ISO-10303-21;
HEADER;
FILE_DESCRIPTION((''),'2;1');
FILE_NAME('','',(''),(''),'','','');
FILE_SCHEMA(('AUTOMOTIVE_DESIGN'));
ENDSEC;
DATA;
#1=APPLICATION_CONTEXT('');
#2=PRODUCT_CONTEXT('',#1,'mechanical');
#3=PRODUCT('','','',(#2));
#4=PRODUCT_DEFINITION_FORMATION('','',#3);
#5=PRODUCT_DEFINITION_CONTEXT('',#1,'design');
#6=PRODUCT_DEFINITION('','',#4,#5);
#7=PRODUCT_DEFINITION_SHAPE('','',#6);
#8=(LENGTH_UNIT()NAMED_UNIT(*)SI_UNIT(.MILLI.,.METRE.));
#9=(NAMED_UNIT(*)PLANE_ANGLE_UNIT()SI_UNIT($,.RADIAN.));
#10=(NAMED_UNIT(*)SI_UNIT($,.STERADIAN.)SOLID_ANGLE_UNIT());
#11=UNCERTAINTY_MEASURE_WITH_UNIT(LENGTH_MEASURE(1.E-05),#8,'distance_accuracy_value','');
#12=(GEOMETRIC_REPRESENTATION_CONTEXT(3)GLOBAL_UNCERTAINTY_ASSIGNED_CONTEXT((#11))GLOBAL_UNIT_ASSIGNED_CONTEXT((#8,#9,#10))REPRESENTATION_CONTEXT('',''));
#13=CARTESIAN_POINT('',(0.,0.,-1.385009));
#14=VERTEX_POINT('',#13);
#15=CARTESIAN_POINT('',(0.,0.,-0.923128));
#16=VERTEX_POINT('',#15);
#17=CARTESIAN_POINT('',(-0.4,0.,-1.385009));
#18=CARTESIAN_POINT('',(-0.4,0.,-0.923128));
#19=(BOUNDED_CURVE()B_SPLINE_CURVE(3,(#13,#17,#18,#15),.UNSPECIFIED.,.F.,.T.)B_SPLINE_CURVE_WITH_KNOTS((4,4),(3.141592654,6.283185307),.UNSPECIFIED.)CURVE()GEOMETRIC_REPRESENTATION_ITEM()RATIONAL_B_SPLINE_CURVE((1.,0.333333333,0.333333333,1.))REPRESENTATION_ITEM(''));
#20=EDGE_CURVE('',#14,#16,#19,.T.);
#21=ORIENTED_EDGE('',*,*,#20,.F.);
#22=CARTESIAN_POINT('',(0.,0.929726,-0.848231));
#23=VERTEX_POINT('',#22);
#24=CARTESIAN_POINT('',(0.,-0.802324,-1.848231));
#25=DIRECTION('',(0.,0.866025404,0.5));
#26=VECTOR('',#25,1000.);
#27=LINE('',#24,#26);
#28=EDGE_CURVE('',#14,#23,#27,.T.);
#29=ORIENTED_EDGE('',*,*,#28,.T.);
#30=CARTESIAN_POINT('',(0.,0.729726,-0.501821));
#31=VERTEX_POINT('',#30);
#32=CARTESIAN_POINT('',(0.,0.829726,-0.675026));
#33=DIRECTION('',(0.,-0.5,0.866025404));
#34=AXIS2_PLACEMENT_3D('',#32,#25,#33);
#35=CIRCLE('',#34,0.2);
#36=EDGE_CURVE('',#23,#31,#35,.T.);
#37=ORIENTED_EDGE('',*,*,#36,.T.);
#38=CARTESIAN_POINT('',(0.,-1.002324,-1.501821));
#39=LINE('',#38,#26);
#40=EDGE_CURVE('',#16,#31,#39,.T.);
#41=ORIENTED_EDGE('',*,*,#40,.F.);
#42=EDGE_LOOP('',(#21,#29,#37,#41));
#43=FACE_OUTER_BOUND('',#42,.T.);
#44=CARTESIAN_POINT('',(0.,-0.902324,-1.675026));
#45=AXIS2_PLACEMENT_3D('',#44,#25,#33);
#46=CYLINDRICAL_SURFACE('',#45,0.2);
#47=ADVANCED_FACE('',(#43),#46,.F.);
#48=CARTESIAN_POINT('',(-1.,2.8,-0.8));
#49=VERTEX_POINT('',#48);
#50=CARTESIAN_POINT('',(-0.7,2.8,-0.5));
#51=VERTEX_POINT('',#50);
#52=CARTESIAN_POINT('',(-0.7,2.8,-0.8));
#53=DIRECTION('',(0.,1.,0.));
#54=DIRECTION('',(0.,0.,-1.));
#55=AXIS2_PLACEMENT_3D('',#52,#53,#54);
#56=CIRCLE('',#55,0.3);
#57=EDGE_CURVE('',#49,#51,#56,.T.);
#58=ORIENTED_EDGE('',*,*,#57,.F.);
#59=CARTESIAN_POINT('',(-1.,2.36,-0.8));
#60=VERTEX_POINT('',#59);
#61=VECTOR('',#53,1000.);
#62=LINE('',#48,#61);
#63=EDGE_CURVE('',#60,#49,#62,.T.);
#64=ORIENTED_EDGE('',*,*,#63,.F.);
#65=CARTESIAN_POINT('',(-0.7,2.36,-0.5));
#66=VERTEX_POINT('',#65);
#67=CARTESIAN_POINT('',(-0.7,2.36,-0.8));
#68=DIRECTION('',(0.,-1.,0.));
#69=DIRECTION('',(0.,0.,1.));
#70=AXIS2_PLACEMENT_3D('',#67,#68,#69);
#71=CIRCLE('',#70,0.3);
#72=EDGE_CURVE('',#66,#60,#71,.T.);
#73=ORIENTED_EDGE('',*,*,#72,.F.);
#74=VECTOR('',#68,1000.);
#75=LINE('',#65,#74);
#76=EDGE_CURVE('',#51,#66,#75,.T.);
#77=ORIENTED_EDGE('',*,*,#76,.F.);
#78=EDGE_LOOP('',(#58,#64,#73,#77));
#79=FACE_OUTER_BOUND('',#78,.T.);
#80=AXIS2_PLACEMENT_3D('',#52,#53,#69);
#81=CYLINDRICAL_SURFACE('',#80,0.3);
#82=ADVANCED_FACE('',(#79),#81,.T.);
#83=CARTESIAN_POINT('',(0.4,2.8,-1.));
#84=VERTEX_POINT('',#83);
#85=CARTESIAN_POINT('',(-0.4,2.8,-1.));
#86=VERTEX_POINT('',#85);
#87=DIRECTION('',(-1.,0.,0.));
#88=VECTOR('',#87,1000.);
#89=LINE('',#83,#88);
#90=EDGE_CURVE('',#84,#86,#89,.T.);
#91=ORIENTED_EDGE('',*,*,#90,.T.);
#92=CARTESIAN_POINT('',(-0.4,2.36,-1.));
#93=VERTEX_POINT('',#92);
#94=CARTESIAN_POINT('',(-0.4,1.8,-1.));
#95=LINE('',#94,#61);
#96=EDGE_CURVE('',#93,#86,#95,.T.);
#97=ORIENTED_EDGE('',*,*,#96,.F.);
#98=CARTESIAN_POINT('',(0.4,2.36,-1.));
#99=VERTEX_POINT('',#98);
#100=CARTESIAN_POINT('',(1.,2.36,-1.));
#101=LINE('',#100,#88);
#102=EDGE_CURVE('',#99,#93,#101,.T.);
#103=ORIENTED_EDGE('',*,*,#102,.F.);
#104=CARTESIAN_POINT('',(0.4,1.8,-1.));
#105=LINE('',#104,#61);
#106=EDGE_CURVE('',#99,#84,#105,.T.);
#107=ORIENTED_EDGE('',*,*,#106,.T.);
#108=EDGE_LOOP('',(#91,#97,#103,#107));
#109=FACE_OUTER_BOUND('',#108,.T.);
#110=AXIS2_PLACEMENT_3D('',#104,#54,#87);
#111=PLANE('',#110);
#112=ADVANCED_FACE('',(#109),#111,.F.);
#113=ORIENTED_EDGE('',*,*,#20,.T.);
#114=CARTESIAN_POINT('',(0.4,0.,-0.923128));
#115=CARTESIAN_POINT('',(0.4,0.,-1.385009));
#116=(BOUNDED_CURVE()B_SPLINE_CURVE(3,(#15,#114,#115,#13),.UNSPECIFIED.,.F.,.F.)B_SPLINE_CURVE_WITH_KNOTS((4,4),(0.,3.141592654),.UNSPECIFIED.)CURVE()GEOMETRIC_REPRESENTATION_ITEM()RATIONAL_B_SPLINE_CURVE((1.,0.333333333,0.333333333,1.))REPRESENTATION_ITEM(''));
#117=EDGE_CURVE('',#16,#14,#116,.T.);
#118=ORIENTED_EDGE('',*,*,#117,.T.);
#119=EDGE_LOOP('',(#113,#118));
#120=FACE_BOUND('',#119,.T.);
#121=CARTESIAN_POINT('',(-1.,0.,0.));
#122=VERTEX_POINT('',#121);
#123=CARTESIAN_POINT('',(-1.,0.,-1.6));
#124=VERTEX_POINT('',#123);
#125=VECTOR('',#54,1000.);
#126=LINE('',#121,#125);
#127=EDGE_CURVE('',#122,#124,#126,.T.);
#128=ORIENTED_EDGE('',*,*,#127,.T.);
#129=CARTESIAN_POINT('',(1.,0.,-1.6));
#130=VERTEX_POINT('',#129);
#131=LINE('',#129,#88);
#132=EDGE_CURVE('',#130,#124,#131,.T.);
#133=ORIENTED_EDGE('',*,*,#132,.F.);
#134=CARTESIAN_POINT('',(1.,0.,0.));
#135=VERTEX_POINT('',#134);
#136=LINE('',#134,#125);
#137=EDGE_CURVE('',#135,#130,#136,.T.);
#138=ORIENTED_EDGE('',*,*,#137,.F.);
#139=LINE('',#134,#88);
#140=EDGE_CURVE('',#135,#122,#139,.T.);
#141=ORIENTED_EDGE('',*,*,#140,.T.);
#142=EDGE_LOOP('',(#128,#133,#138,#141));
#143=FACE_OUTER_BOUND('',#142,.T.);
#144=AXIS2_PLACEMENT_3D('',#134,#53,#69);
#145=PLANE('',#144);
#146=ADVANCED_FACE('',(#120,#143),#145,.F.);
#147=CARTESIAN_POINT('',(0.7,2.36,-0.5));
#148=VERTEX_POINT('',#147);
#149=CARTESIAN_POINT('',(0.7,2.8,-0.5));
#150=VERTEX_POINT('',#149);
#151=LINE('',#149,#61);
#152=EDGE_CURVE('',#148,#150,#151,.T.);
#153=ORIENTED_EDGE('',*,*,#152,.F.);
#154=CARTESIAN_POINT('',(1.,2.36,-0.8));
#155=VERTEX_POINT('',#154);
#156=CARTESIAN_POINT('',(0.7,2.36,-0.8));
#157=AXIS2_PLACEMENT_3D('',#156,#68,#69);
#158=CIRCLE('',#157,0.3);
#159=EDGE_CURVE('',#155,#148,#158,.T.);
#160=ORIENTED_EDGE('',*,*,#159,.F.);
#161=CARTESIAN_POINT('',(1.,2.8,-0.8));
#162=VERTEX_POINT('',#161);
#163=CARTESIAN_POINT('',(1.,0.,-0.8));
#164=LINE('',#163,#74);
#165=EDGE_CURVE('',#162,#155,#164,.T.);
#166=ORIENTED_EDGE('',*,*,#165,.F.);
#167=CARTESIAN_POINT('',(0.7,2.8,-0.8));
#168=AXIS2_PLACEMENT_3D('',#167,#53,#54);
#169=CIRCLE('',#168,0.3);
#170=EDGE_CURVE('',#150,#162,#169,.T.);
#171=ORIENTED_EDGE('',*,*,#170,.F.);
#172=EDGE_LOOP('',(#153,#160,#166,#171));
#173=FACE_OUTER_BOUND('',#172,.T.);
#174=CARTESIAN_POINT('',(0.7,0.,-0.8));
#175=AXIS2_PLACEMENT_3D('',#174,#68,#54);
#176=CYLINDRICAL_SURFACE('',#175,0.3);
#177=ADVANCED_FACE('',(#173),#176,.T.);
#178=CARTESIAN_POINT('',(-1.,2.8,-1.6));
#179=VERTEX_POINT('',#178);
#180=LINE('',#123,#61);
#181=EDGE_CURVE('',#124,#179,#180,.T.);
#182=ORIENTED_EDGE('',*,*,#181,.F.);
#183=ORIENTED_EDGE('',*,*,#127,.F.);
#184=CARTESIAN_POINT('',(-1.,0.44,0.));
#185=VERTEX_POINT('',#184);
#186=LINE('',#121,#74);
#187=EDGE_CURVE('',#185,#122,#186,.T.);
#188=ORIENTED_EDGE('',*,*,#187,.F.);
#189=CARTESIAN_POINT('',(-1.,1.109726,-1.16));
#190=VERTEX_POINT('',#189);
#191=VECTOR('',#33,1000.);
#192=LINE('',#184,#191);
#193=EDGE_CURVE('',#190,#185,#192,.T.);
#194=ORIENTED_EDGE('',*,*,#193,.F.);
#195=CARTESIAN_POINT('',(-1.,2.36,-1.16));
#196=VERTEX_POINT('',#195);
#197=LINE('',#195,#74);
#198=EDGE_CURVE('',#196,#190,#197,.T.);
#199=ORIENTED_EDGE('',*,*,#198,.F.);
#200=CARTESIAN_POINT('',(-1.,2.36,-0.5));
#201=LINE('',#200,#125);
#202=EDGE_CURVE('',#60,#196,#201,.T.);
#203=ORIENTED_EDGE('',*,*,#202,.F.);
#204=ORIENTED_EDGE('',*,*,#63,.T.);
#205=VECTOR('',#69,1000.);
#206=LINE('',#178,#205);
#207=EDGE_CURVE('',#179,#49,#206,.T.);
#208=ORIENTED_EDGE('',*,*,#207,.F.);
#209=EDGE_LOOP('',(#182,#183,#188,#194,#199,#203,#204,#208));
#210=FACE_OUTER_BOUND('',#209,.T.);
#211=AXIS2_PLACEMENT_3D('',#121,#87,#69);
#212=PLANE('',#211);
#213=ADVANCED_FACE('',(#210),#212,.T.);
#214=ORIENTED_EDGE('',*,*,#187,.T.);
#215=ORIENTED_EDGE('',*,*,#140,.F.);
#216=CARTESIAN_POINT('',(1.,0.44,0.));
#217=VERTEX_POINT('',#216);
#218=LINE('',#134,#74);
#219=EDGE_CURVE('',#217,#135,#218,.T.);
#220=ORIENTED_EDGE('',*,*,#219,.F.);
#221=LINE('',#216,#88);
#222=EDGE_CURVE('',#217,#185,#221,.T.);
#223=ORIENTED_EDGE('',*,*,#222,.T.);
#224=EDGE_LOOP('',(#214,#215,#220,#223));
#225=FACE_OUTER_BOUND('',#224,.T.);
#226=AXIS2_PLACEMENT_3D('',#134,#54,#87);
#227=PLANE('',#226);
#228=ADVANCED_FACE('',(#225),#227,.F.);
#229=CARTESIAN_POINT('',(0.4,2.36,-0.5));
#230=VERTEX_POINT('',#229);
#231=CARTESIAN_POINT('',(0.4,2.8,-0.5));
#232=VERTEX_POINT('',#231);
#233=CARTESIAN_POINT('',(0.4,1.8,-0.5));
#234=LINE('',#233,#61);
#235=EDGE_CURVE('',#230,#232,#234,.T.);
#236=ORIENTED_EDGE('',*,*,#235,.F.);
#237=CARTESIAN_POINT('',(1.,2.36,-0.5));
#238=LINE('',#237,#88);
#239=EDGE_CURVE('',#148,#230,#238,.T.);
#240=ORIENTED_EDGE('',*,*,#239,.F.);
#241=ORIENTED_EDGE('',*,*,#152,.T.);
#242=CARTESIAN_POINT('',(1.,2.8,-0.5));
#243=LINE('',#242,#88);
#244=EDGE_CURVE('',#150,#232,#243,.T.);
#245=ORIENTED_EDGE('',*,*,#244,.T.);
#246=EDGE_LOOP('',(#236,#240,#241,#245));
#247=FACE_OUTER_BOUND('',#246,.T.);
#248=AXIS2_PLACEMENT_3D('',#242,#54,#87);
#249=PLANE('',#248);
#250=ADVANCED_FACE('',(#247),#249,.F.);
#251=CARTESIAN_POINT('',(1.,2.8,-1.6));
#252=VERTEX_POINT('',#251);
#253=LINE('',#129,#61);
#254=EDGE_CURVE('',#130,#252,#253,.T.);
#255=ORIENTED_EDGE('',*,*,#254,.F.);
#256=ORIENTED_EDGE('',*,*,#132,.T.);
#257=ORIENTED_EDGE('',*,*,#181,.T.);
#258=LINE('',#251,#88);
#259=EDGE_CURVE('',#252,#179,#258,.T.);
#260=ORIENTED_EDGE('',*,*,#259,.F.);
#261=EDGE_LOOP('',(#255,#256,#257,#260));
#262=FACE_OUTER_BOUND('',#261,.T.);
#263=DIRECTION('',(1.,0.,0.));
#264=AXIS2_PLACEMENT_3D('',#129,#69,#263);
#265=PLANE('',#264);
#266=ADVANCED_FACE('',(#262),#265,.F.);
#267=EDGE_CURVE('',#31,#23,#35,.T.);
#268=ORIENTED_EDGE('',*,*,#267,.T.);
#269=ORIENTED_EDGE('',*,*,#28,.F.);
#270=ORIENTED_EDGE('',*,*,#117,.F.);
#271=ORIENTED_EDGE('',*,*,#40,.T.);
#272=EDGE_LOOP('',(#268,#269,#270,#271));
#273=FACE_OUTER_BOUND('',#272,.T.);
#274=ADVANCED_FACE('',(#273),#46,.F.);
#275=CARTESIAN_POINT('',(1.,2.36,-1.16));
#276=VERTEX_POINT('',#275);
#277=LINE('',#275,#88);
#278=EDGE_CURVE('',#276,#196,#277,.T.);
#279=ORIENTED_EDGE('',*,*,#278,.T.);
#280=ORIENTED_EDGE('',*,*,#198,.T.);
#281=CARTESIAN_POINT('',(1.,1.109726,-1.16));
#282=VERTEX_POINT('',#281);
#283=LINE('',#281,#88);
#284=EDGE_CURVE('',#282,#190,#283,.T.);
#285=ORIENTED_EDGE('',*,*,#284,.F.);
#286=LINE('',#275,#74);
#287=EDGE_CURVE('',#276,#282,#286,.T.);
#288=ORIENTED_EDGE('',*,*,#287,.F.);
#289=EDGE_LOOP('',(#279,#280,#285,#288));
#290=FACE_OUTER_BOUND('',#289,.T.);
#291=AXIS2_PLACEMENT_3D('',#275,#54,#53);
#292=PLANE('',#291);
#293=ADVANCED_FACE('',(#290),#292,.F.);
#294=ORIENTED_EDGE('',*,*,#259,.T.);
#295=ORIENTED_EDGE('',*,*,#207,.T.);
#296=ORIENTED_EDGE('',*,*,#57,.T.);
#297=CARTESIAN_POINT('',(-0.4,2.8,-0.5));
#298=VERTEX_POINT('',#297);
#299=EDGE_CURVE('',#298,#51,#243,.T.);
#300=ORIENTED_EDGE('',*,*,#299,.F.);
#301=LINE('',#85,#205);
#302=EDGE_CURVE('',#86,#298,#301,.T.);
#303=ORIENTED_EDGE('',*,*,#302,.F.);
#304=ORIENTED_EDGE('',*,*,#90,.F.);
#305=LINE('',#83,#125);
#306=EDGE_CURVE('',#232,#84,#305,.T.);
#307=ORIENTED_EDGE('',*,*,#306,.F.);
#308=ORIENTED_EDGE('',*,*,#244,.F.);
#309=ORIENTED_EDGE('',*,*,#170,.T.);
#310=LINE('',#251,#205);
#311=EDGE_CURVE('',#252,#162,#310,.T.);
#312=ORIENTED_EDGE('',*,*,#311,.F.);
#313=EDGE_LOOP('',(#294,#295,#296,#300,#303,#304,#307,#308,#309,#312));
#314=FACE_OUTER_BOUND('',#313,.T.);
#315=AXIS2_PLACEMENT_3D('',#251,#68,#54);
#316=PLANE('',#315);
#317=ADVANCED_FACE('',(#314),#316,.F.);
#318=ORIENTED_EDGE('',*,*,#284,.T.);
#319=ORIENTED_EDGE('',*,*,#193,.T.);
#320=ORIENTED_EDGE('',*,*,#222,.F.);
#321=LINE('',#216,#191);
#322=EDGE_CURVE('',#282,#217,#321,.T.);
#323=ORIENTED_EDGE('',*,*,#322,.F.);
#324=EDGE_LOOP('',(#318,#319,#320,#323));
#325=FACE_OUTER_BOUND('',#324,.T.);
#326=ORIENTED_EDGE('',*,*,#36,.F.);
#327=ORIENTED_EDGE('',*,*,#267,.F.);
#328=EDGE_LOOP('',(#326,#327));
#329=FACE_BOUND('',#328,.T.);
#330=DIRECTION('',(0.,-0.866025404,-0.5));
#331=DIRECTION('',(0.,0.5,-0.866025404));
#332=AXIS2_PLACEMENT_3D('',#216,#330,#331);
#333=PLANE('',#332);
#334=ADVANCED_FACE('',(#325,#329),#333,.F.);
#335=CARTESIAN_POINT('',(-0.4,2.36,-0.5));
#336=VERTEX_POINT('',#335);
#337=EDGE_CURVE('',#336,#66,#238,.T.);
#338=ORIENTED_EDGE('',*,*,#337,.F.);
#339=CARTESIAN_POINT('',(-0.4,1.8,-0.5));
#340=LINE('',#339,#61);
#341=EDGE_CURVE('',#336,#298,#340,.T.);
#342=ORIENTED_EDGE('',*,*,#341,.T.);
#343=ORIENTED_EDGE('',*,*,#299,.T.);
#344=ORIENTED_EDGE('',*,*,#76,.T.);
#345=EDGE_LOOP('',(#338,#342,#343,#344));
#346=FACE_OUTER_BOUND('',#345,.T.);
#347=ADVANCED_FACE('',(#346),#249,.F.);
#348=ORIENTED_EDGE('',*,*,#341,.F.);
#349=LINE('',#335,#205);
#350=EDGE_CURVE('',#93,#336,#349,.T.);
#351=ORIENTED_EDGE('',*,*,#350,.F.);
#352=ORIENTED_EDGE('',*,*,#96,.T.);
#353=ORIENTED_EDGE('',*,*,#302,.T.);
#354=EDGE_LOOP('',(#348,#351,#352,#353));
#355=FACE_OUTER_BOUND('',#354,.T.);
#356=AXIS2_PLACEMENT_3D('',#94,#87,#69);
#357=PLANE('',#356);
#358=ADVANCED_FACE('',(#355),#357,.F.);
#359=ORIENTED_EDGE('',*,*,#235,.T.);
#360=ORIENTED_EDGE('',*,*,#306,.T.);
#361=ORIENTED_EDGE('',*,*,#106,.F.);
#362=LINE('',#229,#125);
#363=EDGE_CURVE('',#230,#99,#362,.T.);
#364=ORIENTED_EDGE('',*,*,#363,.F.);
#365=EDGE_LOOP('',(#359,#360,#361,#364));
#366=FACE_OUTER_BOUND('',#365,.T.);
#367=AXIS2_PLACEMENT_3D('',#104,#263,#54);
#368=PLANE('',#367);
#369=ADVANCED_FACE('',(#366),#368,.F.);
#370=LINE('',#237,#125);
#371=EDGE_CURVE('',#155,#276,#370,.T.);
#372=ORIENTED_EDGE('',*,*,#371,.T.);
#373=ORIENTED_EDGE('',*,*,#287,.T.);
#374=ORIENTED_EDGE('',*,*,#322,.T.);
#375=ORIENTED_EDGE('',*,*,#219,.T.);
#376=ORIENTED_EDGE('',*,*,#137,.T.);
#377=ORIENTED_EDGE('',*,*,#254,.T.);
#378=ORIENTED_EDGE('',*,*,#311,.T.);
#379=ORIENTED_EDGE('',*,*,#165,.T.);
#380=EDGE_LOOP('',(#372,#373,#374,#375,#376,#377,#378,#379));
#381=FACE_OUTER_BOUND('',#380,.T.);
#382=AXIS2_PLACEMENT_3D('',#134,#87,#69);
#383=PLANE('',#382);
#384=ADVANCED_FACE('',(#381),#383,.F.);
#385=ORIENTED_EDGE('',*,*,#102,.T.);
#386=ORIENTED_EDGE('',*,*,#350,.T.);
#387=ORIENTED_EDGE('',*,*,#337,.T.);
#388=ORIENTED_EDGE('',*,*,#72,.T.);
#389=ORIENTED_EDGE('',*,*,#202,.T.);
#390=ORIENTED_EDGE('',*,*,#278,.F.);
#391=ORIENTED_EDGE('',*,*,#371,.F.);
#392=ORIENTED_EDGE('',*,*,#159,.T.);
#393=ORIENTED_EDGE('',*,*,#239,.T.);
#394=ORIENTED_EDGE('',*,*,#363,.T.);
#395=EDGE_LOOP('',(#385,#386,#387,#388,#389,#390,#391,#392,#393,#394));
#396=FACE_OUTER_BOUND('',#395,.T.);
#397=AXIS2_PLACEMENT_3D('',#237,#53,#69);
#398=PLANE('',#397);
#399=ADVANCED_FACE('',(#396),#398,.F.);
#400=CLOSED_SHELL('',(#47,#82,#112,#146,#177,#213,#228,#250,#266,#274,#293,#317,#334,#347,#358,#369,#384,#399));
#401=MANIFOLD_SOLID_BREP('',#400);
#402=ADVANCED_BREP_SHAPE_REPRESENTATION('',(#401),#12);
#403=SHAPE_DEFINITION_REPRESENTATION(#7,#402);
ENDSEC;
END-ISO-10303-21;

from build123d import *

# Parameters (mm, degrees)
L_BRACKET_BODY_2MM_DEPTH        = 1
UPRIGHT_SLOT_SKETCH_W           = 0.8
UPRIGHT_SLOT_SKETCH_H           = 0.5
UPRIGHT_SLOT_CUT_1MM_DEEP_DEPTH = 1
CORNER_FILLET_R0_3_A_R          = 0.3
CORNER_FILLET_R0_3_B_R          = 0.3
ANGLED_FACE_HOLE_SKETCH_R       = 0.2
ANGLED_FACE_HOLE_CUT_DEPTH      = 2


with BuildPart() as part:
    # L Profile Sketch → L Bracket Body 2mm (new, symmetric)
    with BuildSketch(Plane(origin=(0, 0, 0), x_dir=(0, 0, -1), z_dir=(1, 0, 0))):
        Polygon((0, 0), (1.6, 0), (1.6, 2.8), (0.5, 2.8), (0.5, 2.36), (1.16, 2.36), (1.16, 1.109726312), (0, 0.44), align=None)
    extrude(amount=L_BRACKET_BODY_2MM_DEPTH, both=True)

    # Upright Slot Sketch → Upright Slot Cut 1mm Deep (cut)
    with BuildSketch(Plane(origin=(0, 2.8, 0), x_dir=(1, 0, 0), z_dir=(0, 1, 0))):
        with Locations((0, 0.75)):
            Rectangle(UPRIGHT_SLOT_SKETCH_W, UPRIGHT_SLOT_SKETCH_H)
    extrude(amount=-UPRIGHT_SLOT_CUT_1MM_DEEP_DEPTH, mode=Mode.SUBTRACT)

    # Corner Fillet R0.3 A
    corner_fillet_r0_3_a_edges = [part.edges().sort_by_distance(p)[0] for p in [
        (1, 2.58, -0.5),
    ]]
    fillet(corner_fillet_r0_3_a_edges, radius=CORNER_FILLET_R0_3_A_R)

    # Corner Fillet R0.3 B
    corner_fillet_r0_3_b_edges = [part.edges().sort_by_distance(p)[0] for p in [
        (-1, 2.58, -0.5),
    ]]
    fillet(corner_fillet_r0_3_b_edges, radius=CORNER_FILLET_R0_3_B_R)

    # Angled Face Hole Sketch → Angled Face Hole Cut (cut)
    with BuildSketch(Plane(origin=(0, 0.33, 0.190525589), x_dir=(1, 0, 0), z_dir=(0, 0.8660254037844379, 0.5000000000000014))):
        with Locations(Location((0, 0.999452625, 0), (0, 0, 270))):
            Circle(ANGLED_FACE_HOLE_SKETCH_R)
    extrude(amount=-ANGLED_FACE_HOLE_CUT_DEPTH, mode=Mode.SUBTRACT)


solid = part.part
